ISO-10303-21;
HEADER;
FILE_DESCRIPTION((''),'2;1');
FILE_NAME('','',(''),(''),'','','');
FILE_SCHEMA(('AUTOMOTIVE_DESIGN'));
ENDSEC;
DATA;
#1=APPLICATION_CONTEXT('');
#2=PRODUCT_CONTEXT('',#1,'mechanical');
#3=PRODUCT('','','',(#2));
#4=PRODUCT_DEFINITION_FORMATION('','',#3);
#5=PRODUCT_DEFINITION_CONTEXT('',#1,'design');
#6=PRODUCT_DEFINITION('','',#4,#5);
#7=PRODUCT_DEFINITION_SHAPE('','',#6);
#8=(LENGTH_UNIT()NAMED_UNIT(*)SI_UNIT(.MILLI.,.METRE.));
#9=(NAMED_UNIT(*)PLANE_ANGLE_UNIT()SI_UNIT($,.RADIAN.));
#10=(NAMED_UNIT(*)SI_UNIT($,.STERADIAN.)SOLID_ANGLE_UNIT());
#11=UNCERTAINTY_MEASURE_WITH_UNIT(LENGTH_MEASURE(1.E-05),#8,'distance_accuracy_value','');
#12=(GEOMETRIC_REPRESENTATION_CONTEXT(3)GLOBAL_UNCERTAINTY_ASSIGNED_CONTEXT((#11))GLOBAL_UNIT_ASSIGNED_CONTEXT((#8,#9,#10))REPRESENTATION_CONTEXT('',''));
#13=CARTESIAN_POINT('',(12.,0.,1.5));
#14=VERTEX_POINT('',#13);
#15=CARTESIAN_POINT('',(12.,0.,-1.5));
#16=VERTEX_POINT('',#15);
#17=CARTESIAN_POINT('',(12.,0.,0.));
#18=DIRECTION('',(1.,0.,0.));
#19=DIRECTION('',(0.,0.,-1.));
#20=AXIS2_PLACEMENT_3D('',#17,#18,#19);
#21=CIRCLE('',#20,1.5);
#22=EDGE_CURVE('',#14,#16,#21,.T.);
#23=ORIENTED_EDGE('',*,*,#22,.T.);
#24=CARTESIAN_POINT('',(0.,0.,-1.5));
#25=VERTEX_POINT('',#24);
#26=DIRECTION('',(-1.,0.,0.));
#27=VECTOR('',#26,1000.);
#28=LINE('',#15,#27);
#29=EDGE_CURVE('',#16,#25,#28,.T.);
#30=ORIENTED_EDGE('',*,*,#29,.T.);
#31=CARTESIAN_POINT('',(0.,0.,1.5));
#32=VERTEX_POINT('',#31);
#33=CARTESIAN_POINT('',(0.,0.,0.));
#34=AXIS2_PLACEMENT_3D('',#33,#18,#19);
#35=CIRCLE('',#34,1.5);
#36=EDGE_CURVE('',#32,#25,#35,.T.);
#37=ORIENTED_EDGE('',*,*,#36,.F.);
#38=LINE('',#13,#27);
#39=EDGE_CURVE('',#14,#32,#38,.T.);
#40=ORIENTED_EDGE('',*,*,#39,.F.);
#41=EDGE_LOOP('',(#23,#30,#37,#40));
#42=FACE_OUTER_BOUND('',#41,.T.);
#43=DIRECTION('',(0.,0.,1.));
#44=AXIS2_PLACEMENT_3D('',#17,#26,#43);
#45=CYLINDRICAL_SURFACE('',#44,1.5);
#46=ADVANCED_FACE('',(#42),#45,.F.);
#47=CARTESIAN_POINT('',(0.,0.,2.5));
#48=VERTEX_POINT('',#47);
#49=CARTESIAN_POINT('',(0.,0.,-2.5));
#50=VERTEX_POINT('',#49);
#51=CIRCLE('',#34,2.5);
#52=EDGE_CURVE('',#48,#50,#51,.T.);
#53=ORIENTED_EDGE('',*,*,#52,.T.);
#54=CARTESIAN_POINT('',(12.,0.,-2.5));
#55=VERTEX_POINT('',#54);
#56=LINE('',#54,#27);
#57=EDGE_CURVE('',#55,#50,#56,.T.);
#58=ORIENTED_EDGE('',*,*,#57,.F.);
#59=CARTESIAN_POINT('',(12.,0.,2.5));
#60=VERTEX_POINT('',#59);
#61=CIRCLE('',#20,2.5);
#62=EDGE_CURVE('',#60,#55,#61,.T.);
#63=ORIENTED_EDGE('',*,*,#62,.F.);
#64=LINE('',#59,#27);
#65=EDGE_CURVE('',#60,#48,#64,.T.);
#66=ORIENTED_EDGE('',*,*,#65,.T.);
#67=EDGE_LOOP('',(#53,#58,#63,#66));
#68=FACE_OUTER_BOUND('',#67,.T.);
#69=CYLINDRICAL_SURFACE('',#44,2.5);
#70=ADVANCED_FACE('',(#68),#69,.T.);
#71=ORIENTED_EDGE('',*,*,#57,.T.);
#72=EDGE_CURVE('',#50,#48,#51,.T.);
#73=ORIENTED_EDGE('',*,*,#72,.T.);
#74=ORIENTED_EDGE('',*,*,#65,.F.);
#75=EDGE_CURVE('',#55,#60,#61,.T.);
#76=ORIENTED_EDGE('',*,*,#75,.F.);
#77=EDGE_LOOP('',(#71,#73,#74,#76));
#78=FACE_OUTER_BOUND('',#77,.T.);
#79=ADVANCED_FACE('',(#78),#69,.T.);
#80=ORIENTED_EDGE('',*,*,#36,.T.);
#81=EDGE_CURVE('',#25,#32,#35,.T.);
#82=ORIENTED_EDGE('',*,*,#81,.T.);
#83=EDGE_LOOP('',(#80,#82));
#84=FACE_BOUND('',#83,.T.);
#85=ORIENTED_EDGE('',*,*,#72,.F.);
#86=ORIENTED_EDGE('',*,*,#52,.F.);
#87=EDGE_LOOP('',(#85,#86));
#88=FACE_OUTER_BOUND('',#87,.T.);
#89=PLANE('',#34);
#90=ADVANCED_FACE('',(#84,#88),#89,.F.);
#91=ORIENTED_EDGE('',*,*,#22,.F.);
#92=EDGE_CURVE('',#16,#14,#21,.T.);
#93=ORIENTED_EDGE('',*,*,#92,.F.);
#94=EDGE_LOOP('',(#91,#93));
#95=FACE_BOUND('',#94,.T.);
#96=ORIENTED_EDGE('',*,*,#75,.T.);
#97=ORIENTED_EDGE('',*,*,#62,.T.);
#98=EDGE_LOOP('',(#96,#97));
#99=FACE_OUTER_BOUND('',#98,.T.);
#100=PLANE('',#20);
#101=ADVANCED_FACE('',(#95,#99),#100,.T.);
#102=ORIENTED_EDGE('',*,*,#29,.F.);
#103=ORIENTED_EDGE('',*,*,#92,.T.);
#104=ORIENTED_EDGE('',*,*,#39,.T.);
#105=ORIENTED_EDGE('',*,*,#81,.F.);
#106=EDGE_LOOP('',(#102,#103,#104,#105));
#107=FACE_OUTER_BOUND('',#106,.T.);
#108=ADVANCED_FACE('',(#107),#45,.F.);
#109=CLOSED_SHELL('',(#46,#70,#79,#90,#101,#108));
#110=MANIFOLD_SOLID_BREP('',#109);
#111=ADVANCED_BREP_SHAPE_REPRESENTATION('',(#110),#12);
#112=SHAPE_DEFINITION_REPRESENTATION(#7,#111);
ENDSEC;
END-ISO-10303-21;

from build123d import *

# Parameters (mm, degrees)
SKETCH_1_R      = 2.5
SKETCH_1_R_2    = 1.5
EXTRUDE_1_DEPTH = 12


with BuildPart() as part:
    # 草图1 → 凸台-拉伸1 (new body)
    with BuildSketch(Plane(origin=(0, 0, 0), x_dir=(0, 0, -1), z_dir=(1, 0, 0))):
        Circle(SKETCH_1_R)
        Circle(SKETCH_1_R_2, mode=Mode.SUBTRACT)
    extrude(amount=EXTRUDE_1_DEPTH)


solid = part.part
